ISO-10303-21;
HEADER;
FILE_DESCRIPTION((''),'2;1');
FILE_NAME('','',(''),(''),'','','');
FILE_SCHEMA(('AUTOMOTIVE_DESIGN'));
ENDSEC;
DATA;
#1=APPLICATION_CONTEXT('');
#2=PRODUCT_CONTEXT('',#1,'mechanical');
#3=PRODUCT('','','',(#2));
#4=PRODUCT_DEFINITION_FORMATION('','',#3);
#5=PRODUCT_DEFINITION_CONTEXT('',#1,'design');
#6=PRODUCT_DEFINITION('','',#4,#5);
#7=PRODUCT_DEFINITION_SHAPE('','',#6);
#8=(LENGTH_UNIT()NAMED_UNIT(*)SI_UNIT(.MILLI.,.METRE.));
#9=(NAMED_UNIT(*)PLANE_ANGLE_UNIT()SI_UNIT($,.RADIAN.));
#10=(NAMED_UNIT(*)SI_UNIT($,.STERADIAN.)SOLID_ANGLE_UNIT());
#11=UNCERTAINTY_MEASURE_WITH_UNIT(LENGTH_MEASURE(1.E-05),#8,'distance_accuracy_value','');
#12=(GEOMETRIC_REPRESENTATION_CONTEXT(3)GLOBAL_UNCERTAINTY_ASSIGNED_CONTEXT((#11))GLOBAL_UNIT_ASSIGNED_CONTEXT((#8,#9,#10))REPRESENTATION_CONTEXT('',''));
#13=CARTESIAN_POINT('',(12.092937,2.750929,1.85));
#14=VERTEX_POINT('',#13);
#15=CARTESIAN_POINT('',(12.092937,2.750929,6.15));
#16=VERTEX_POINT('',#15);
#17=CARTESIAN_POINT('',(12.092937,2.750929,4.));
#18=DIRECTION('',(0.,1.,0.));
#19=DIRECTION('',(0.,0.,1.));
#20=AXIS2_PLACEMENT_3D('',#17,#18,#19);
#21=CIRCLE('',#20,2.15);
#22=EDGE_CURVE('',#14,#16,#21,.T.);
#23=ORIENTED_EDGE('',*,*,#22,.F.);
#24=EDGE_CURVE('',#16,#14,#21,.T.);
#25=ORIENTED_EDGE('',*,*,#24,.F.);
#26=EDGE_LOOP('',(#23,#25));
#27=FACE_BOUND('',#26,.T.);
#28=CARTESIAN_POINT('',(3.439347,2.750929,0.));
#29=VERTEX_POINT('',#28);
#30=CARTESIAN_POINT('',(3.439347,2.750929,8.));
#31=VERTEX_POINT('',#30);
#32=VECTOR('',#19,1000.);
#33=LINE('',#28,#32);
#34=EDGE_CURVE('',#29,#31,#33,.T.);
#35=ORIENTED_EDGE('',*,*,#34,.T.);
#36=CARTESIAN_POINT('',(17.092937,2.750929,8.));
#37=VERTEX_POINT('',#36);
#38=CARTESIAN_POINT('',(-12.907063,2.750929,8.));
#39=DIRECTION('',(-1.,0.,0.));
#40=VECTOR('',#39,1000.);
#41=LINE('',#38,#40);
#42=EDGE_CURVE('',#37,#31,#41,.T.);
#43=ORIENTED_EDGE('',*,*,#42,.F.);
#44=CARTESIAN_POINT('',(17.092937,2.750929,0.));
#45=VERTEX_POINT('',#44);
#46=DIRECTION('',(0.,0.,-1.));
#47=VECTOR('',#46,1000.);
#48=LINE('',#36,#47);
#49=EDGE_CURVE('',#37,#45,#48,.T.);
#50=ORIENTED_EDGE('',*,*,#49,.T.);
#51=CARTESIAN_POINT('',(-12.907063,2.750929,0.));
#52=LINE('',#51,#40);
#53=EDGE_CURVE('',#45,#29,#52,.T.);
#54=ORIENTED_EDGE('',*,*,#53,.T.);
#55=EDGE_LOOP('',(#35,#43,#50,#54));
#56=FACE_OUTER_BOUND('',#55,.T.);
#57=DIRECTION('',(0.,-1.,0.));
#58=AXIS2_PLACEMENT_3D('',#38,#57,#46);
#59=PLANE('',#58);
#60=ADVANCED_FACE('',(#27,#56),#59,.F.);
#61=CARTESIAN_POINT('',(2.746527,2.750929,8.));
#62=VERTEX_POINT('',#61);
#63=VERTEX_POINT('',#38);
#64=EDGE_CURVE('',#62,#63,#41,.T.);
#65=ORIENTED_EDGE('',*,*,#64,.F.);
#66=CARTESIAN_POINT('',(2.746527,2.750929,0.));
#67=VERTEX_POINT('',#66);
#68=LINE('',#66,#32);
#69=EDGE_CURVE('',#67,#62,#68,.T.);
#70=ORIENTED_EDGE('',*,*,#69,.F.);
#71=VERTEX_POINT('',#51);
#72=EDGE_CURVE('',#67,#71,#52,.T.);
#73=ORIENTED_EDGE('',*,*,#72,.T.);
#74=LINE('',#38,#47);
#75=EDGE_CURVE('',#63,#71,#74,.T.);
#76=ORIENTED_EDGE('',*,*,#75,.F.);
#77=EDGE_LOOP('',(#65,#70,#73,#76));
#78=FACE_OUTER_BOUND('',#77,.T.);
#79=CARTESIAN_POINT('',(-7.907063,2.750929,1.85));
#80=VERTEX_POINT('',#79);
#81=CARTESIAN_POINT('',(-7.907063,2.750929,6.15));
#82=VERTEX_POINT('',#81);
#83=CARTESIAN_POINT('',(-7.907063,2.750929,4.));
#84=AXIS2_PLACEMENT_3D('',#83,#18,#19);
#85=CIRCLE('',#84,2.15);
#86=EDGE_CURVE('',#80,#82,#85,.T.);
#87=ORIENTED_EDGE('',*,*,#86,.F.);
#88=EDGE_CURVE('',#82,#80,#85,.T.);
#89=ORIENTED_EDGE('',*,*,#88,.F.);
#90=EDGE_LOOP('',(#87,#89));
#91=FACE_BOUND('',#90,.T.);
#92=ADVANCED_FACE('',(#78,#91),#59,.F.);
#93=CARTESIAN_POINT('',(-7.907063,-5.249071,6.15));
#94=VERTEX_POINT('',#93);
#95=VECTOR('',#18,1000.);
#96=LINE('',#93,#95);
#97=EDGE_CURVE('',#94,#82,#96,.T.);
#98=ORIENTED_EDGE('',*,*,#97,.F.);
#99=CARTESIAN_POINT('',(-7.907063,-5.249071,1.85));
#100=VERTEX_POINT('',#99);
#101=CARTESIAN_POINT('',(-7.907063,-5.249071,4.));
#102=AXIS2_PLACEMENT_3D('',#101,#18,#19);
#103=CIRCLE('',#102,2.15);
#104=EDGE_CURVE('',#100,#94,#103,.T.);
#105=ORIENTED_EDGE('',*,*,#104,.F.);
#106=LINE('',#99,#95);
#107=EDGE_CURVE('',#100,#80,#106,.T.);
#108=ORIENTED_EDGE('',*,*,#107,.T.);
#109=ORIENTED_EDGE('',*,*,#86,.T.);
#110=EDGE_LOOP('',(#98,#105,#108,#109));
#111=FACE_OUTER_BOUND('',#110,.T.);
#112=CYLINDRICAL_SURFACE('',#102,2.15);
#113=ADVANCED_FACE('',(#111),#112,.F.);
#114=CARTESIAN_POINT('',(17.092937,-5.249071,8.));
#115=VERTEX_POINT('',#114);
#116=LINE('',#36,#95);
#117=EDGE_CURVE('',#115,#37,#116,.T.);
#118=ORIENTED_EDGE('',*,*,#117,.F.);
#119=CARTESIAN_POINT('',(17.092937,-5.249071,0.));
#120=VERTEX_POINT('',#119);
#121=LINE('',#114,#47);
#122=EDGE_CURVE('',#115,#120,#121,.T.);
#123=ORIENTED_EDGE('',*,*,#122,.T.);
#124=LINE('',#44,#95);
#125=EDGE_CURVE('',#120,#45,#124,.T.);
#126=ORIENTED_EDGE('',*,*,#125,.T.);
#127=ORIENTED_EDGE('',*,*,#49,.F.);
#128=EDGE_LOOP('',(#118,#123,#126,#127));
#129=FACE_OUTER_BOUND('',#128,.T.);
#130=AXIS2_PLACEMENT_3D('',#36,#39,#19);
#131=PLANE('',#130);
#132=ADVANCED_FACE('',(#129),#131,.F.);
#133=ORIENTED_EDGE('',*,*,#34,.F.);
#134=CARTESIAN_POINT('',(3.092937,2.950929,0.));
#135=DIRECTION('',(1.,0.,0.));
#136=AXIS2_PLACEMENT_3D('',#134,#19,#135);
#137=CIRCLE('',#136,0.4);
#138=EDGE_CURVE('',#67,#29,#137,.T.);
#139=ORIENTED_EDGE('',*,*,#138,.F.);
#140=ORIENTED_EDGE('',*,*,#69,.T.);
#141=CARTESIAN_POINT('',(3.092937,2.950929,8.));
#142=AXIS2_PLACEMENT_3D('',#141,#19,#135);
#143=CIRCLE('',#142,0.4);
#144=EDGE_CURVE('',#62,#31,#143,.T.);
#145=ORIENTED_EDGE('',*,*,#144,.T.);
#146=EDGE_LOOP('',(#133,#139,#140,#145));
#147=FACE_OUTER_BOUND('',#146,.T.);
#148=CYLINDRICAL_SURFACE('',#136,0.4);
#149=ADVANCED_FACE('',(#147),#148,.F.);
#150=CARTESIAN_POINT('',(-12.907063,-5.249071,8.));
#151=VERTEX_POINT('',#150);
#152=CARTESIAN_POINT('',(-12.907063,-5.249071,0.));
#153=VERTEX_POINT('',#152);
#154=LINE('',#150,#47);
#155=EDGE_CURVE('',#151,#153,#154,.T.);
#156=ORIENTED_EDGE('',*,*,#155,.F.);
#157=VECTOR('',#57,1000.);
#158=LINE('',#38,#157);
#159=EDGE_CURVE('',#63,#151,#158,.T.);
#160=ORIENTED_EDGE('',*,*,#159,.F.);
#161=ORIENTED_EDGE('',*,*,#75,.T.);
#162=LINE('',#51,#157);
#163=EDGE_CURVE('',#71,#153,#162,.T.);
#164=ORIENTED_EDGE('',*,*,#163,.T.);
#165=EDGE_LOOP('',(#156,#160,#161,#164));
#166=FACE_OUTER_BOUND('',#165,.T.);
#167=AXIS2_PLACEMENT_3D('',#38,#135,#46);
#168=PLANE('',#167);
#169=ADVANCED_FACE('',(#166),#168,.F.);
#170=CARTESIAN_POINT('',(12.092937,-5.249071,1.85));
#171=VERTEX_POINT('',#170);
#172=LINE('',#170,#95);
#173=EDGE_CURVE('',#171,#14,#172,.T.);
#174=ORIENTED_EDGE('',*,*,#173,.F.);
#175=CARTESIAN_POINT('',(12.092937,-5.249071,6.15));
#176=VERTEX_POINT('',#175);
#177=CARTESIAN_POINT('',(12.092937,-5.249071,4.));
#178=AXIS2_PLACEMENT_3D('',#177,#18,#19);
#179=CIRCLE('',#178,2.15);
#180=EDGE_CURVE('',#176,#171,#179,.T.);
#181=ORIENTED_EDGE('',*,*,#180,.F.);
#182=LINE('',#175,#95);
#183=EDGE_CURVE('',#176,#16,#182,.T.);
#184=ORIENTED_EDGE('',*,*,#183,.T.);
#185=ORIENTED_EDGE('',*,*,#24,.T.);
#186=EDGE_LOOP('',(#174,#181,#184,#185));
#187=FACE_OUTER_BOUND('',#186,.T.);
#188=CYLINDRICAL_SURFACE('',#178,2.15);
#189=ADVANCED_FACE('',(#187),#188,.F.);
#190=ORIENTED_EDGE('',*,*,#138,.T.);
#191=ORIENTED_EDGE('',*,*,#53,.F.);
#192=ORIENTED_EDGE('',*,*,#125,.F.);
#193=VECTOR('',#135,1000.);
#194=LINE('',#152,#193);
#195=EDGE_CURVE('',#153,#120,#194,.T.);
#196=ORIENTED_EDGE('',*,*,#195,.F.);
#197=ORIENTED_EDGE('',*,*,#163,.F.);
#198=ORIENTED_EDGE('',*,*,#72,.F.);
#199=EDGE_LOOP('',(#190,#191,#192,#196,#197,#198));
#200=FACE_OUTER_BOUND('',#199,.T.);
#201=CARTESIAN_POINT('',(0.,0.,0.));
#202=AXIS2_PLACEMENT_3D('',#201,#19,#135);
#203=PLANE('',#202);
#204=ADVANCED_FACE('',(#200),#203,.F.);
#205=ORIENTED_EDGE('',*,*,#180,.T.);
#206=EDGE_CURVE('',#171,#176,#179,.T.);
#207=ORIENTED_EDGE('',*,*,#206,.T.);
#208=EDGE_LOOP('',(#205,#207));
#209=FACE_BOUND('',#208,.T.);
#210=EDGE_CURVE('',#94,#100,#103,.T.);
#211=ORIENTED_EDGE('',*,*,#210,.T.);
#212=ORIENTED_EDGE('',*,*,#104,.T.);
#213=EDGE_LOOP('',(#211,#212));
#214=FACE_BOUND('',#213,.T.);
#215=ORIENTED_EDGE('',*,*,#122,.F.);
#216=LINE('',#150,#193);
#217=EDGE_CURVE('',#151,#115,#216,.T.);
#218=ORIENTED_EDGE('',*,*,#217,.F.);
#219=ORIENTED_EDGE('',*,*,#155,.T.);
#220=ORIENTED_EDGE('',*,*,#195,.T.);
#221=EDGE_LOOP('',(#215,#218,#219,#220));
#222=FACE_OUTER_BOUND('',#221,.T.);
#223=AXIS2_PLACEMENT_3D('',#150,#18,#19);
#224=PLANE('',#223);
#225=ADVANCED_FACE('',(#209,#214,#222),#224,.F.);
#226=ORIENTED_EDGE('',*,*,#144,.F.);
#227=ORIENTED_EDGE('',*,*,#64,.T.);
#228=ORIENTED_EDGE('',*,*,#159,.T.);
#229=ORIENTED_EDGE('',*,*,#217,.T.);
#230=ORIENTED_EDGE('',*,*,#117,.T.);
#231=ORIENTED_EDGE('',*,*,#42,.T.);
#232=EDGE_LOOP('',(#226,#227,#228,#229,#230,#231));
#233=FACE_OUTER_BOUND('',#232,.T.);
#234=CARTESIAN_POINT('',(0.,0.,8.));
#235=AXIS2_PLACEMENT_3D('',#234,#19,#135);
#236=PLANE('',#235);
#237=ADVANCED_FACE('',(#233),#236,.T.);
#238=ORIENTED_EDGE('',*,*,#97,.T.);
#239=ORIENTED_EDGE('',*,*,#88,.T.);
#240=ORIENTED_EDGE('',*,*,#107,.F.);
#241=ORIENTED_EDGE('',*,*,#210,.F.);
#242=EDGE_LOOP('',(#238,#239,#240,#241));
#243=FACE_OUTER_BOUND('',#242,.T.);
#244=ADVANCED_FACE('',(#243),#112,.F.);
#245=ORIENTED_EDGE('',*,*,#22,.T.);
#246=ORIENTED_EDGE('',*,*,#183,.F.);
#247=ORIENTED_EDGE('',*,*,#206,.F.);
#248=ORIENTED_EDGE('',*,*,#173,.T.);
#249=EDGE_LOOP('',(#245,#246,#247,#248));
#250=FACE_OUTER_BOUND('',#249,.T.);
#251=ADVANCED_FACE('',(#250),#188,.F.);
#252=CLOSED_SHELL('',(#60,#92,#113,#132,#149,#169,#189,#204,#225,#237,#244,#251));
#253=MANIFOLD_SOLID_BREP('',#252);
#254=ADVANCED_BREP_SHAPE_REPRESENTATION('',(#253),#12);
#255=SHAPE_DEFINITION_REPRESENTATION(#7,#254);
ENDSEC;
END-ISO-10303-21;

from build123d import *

# Parameters (mm, degrees)
SKETCH_1_W          = 30
SKETCH_1_H          = 8
EXTRUDE_1_DEPTH     = 8
SKETCH_2_R          = 2.15
CUT_EXTRUDE_1_DEPTH = 21.498011819
CUT_EXTRUDE_2_DEPTH = 20.588803717


with BuildPart() as part:
    # 草图1 → 凸台-拉伸1 (new body)
    with BuildSketch(Plane.XY):
        with Locations((2.092936803, -1.249070632)):
            Rectangle(SKETCH_1_W, SKETCH_1_H)
    extrude(amount=EXTRUDE_1_DEPTH)

    # 草图2 → 切除-拉伸1 (cut, through all)
    with BuildSketch(Plane(origin=(0, 2.750929368, 0), x_dir=(1, 0, 0), z_dir=(0, 1, 0))):
        with Locations(Location((-7.907063197, -4, 0), (0, 0, 270))):
            Circle(SKETCH_2_R)
        with Locations(Location((12.092936803, -4, 0), (0, 0, 270))):
            Circle(SKETCH_2_R)
    extrude(amount=-CUT_EXTRUDE_1_DEPTH, mode=Mode.SUBTRACT)

    # 草图3 → 切除-拉伸2 (cut, through all)
    with BuildSketch(Plane.XY.offset(8)):
        with BuildLine():
            Line((2.746526641, 2.750929368), (3.439346964, 2.750929368))
            ThreePointArc((3.439346964, 2.750929368), (3.092936803, 2.550929368), (2.746526641, 2.750929368))
        make_face()
    extrude(amount=-CUT_EXTRUDE_2_DEPTH, mode=Mode.SUBTRACT)


solid = part.part
